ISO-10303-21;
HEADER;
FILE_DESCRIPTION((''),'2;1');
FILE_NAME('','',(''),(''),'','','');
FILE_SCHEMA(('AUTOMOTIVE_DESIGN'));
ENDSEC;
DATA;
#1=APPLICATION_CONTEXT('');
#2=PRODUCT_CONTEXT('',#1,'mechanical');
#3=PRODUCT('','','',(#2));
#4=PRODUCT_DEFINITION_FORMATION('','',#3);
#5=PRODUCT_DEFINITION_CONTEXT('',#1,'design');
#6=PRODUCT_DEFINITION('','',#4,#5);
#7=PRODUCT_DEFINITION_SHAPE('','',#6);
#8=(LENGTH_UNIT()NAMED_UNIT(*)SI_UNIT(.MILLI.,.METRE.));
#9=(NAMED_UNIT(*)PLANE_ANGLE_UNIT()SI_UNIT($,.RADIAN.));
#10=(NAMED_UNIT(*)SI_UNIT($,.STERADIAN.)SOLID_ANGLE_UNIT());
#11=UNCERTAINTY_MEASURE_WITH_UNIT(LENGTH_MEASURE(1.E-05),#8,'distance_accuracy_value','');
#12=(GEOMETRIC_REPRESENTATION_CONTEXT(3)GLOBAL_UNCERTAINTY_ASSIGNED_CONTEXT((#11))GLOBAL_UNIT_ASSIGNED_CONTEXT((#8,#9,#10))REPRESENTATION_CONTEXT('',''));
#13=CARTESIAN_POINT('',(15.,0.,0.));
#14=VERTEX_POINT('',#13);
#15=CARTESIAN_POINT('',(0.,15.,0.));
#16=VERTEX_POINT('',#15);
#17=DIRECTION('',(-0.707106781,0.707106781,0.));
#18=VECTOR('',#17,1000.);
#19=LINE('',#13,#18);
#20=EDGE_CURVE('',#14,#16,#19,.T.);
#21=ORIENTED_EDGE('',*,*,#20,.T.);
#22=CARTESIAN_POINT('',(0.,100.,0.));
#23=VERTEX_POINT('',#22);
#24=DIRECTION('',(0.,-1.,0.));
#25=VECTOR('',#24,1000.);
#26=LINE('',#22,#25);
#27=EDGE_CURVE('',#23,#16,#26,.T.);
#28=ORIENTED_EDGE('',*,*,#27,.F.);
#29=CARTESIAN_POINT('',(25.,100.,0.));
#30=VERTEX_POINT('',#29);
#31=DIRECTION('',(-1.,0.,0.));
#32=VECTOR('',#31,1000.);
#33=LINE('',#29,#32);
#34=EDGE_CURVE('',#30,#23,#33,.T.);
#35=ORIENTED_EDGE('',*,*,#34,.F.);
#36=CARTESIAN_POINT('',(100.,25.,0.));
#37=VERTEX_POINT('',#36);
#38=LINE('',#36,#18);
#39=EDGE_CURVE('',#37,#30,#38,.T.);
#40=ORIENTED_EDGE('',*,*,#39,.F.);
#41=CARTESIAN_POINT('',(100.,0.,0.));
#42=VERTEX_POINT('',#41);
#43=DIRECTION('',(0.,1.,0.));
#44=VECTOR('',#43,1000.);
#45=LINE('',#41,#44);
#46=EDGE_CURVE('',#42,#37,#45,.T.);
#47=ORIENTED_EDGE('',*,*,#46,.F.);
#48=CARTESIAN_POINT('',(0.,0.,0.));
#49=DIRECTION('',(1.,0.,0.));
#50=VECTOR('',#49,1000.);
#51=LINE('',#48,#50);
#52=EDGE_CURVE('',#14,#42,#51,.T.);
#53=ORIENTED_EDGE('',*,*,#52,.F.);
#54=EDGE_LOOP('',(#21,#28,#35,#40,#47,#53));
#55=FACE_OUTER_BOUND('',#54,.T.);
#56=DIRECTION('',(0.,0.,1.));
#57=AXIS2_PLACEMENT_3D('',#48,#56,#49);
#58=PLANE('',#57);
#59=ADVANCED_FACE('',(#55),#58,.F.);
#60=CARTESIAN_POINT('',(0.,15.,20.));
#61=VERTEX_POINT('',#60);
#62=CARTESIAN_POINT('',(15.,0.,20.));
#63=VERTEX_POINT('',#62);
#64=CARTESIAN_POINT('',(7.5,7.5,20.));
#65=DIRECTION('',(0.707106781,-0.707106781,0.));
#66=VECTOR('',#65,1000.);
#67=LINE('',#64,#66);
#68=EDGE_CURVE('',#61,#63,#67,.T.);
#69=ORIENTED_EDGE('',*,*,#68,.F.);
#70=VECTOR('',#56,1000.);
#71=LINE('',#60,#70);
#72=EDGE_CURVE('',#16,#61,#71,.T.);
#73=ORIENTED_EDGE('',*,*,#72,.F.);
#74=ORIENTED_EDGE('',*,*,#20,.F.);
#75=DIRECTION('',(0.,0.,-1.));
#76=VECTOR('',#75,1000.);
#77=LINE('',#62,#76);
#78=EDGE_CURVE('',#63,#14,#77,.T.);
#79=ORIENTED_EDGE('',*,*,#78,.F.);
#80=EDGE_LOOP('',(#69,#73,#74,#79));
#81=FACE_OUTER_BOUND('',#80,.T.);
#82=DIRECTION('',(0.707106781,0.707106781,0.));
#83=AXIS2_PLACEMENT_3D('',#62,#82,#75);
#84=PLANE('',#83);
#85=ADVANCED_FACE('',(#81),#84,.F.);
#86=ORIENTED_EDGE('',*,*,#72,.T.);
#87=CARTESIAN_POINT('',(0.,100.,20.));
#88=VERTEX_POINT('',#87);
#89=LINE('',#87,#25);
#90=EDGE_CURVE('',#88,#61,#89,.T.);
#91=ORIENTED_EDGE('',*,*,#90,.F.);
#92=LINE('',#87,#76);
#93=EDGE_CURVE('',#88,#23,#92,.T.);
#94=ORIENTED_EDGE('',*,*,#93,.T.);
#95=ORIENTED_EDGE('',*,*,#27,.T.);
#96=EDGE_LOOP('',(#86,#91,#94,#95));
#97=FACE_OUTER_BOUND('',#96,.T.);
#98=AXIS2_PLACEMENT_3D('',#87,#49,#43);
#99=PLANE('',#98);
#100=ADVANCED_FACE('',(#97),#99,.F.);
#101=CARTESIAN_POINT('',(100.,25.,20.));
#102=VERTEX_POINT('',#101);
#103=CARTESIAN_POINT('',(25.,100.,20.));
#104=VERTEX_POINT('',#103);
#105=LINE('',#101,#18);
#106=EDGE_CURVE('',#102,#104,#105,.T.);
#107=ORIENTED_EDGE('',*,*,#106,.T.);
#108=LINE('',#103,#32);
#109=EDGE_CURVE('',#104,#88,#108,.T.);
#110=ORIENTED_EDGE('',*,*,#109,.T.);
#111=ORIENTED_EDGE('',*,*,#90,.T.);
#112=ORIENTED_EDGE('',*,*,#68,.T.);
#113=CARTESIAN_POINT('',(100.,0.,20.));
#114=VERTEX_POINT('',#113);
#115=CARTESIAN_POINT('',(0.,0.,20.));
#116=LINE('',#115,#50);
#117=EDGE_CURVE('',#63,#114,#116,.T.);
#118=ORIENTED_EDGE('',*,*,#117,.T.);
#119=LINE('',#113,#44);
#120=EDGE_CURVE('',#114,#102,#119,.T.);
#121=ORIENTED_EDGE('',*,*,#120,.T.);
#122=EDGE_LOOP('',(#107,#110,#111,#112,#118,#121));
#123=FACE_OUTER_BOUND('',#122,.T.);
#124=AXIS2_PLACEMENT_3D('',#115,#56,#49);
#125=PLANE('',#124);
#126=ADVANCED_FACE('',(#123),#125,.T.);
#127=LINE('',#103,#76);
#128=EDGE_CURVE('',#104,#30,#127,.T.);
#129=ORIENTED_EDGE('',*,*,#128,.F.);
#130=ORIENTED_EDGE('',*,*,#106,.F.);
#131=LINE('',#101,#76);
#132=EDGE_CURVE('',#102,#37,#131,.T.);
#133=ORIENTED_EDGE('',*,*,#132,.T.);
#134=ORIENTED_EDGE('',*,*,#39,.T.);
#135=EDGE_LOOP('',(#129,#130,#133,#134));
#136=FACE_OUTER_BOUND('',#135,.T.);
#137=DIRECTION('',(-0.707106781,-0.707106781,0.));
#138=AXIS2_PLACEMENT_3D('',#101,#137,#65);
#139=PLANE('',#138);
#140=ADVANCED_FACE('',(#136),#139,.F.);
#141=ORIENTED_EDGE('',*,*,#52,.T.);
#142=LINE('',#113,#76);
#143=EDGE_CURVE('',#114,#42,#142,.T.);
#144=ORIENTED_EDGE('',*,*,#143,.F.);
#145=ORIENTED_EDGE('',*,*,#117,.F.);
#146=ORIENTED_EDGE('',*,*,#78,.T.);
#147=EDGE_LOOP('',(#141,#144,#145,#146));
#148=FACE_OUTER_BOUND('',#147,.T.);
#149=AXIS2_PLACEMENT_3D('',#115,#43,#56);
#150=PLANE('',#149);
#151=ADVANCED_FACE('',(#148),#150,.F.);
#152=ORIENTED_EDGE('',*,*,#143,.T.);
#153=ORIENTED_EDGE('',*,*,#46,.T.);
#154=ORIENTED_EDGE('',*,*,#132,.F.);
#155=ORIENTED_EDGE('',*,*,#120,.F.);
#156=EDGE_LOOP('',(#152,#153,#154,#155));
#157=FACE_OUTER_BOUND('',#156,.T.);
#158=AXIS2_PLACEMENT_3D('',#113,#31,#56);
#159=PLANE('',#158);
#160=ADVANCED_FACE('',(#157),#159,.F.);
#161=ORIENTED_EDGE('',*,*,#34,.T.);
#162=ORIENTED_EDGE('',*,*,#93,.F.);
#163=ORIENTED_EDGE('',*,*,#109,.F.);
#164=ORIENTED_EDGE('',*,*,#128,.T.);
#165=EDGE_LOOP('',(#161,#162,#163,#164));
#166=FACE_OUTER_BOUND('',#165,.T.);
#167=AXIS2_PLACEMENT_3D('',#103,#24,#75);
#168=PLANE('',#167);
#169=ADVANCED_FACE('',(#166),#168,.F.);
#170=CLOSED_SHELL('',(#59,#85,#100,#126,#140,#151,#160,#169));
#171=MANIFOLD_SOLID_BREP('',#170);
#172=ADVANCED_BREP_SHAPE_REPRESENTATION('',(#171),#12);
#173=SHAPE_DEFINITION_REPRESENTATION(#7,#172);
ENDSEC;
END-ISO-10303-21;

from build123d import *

# Parameters (mm, degrees)
BOSS_EXTRUDE1_DEPTH = 20
CHAMFER1_SIZE       = 15


with BuildPart() as part:
    # Sketch1 → Boss-Extrude1 (new body)
    with BuildSketch(Plane.XY):
        Polygon((0, 0), (100, 0), (100, 25), (25, 100), (0, 100), align=None)
    extrude(amount=BOSS_EXTRUDE1_DEPTH)

    # Chamfer1
    chamfer1_edges = [part.edges().sort_by_distance(p)[0] for p in [
        (0, 0, 10),
    ]]
    chamfer(chamfer1_edges, length=CHAMFER1_SIZE)


solid = part.part
